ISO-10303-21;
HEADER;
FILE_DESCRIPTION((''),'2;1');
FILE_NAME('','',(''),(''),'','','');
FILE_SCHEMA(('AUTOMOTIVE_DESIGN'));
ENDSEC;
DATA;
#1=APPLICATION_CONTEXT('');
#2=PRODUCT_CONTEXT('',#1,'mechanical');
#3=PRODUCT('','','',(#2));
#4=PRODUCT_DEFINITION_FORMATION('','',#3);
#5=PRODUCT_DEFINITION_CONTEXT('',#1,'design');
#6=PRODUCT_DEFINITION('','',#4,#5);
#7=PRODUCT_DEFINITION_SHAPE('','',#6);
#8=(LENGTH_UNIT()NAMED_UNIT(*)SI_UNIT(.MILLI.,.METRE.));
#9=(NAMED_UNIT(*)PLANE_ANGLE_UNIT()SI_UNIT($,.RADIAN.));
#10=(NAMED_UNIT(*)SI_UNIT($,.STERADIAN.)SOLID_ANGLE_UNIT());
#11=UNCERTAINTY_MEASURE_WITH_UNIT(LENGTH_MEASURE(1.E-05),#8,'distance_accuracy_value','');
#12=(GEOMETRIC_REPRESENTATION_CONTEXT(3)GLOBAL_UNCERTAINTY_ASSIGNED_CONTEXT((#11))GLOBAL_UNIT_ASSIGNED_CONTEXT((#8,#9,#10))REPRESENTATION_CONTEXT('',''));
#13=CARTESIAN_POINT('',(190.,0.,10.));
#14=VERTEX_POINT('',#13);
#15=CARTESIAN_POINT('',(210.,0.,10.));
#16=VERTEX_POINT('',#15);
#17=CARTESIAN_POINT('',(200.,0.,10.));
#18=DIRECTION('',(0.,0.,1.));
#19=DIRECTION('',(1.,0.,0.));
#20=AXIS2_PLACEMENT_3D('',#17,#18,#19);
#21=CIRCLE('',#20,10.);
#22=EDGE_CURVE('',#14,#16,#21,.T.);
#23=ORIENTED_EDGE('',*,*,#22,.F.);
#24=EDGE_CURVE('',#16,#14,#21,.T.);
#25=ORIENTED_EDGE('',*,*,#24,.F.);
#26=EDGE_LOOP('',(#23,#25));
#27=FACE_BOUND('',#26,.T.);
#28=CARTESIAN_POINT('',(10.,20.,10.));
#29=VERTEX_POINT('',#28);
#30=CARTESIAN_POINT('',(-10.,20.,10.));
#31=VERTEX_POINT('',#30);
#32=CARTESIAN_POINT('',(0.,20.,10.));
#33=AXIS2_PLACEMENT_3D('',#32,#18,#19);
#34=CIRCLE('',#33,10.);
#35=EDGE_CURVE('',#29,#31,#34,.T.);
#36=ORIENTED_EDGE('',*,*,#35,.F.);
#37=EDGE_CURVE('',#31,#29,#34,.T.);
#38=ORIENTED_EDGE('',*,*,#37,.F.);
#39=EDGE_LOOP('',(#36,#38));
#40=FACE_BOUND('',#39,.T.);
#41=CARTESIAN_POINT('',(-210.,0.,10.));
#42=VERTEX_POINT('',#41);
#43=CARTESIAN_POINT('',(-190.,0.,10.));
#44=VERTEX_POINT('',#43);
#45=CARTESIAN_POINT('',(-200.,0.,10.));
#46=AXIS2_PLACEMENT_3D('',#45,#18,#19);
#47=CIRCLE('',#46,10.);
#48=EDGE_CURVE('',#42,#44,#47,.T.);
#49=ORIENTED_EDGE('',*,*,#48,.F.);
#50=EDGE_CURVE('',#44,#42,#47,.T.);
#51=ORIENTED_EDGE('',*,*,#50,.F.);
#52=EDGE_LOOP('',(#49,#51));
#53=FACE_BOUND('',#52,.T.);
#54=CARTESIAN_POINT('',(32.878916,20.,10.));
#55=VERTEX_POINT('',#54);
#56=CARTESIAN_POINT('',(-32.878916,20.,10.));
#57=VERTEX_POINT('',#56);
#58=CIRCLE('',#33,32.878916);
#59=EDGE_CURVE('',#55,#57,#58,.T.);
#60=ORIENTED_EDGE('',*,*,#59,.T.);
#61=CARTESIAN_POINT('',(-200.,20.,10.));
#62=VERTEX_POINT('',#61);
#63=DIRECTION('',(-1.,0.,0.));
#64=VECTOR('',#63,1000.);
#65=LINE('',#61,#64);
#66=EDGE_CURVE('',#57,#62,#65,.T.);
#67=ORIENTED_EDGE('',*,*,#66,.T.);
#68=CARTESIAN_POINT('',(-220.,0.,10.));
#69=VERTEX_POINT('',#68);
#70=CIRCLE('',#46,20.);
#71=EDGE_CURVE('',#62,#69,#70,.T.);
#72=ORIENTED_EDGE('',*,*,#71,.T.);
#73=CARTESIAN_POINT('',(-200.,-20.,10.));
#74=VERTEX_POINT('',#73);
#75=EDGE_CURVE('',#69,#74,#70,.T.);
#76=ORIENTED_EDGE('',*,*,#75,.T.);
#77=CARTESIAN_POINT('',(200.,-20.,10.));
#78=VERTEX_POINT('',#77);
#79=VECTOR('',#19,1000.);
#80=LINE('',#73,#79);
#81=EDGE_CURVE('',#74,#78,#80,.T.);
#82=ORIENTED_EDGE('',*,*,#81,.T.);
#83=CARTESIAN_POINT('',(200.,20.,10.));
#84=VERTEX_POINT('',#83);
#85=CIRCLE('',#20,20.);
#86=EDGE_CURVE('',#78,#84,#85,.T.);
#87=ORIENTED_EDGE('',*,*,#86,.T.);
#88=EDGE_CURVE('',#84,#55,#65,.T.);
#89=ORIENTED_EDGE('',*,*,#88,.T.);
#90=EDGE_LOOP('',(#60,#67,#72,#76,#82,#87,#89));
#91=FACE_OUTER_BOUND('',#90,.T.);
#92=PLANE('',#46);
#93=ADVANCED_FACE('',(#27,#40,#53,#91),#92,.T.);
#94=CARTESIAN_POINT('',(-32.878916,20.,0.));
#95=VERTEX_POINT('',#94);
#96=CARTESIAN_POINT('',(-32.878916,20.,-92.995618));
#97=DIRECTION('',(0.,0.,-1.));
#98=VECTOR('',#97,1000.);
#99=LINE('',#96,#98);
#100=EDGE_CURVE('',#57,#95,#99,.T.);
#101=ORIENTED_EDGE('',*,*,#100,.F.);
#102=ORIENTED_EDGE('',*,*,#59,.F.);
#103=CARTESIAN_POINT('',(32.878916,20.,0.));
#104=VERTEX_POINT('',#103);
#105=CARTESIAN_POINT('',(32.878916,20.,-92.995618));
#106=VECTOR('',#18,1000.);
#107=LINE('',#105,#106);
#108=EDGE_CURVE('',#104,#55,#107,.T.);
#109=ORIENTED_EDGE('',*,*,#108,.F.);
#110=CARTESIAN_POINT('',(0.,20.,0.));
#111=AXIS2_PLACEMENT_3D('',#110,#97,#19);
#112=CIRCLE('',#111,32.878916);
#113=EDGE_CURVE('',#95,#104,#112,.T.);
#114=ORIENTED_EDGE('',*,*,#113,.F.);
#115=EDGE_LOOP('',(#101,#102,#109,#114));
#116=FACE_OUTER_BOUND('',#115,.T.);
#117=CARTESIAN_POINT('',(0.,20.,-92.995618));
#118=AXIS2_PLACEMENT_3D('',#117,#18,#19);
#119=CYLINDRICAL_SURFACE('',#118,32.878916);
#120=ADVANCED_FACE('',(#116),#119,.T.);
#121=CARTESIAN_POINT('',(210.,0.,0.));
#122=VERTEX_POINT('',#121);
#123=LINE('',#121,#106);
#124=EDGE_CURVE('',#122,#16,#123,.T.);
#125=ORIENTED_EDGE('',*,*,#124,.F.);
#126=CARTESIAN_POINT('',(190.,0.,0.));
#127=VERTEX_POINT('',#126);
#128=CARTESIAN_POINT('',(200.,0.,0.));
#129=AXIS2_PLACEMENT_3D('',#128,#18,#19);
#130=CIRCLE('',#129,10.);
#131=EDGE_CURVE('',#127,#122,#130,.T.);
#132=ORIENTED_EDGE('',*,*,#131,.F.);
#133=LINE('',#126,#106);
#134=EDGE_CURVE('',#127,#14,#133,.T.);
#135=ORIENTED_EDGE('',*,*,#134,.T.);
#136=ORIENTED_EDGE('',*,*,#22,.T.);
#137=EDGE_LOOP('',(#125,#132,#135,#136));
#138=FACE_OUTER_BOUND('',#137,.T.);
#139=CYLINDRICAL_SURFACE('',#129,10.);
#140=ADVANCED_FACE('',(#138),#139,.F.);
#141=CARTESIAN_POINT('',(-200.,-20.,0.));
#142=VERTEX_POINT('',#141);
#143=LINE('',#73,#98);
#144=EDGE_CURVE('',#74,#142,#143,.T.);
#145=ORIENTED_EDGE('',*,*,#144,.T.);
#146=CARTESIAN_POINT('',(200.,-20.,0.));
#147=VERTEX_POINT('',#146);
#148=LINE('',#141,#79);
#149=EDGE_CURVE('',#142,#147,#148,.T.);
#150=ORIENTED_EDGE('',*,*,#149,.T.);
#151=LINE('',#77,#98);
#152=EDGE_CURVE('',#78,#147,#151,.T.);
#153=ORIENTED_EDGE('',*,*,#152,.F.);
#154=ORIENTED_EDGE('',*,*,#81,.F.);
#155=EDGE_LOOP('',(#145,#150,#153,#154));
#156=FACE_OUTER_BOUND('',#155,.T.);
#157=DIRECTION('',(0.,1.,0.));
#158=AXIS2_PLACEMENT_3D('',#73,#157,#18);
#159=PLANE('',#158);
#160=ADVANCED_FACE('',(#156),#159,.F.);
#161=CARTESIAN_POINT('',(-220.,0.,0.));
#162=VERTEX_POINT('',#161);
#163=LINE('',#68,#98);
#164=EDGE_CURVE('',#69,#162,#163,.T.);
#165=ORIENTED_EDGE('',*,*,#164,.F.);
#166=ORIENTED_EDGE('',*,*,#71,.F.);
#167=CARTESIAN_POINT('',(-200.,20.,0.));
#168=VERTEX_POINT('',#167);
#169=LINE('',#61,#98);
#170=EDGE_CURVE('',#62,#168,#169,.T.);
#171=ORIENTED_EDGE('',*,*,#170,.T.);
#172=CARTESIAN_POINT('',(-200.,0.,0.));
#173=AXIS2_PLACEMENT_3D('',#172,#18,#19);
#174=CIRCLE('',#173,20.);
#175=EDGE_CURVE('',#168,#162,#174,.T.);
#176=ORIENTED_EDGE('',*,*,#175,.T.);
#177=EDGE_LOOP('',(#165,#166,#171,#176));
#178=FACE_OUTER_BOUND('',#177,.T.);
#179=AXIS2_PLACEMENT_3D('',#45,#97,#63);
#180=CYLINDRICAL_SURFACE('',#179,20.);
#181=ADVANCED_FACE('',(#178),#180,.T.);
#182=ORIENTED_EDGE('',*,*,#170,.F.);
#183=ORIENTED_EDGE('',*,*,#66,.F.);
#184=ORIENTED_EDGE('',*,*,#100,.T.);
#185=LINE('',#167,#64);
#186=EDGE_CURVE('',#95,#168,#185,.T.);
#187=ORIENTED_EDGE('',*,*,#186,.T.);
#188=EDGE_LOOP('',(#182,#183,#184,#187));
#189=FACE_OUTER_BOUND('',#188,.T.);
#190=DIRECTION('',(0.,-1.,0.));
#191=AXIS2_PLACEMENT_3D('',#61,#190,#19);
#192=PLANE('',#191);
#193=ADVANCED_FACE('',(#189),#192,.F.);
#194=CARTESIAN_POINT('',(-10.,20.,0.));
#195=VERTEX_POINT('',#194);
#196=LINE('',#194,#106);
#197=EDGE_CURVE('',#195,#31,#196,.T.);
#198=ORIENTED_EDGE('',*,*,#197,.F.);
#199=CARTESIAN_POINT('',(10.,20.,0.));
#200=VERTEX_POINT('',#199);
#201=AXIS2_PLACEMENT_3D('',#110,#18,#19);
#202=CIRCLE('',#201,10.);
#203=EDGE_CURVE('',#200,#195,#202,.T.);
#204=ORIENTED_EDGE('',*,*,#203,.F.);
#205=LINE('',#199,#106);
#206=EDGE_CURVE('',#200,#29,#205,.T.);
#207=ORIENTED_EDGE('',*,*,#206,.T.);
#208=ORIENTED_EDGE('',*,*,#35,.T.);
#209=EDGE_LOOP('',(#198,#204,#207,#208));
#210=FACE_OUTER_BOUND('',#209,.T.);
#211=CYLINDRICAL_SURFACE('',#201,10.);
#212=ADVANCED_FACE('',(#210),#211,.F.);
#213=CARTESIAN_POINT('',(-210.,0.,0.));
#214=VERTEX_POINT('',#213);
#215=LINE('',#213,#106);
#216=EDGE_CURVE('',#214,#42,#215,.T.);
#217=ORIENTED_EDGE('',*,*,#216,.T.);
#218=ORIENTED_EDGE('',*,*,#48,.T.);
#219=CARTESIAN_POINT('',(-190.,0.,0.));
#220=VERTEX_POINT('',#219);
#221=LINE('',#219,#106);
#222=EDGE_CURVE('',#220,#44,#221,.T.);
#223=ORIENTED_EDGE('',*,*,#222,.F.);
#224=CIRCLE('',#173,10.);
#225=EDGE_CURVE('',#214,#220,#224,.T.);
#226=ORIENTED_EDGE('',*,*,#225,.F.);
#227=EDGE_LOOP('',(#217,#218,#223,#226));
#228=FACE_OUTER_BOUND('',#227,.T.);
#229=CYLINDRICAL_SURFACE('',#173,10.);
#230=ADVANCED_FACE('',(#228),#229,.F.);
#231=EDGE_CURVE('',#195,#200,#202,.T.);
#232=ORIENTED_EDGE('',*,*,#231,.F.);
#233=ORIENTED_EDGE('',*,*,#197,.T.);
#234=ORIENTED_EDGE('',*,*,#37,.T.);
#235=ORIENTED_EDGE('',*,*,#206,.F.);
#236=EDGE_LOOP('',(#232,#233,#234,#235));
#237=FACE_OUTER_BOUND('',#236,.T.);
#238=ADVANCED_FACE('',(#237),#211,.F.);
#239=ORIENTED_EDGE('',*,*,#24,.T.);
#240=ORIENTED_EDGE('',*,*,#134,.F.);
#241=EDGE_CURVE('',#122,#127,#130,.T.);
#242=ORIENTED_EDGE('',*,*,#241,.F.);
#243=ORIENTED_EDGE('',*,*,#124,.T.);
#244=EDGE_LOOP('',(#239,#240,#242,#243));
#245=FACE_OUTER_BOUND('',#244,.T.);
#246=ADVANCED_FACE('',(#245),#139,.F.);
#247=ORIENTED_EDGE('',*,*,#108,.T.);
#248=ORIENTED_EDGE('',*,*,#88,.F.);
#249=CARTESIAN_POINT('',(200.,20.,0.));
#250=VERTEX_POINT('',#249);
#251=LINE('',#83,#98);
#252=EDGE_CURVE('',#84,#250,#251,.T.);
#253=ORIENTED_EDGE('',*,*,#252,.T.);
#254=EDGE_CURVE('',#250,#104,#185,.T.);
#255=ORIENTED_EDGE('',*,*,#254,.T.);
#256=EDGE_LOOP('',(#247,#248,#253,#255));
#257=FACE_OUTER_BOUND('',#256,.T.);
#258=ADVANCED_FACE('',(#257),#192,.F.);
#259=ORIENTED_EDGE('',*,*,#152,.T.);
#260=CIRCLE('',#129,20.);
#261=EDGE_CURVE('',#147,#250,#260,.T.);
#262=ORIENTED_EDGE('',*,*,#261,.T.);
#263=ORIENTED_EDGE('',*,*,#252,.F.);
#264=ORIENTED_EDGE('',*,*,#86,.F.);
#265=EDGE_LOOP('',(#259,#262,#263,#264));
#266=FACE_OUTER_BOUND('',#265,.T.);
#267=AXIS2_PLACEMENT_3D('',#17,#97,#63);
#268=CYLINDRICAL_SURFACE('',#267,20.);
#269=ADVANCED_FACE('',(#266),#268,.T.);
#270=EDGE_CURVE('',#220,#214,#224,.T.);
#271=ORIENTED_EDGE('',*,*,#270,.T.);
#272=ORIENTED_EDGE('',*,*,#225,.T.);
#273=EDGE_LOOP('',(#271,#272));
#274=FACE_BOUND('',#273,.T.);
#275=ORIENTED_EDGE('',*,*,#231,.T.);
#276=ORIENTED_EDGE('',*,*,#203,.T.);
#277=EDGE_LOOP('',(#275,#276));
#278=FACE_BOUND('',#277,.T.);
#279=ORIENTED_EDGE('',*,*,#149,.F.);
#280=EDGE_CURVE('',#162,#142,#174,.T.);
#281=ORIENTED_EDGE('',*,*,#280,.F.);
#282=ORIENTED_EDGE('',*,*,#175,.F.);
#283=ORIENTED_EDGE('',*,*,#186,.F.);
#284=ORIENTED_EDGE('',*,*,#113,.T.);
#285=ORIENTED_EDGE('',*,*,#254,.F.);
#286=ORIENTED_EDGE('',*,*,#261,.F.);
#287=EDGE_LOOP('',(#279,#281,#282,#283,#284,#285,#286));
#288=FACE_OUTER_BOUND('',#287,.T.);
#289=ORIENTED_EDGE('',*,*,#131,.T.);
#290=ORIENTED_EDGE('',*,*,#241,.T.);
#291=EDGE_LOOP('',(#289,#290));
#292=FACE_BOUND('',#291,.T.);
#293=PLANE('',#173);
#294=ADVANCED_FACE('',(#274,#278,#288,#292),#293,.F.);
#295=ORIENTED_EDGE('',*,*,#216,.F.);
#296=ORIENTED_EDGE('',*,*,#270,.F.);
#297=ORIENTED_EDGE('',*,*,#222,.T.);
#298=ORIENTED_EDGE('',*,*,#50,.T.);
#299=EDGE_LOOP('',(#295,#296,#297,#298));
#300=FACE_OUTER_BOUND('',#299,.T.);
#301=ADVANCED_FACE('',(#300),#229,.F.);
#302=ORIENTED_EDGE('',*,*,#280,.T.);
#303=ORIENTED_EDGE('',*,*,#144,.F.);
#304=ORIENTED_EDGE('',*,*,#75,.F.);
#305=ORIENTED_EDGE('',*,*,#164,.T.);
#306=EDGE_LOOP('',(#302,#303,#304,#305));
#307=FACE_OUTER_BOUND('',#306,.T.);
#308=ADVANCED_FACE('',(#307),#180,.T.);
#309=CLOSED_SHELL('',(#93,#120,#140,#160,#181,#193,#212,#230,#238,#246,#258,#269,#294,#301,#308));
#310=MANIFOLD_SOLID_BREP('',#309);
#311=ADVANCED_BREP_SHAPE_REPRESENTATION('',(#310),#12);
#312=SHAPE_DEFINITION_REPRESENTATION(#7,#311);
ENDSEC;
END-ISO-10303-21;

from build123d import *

# Parameters (mm, degrees)
BOSS_EXTRUDE1_DEPTH = 10
SKETCH2_R           = 10
CUT_EXTRUDE1_DEPTH  = 222.133443875
SKETCH4_R           = 32.878916004
BOSS_EXTRUDE2_DEPTH = 10
SKETCH5_R           = 10
CUT_EXTRUDE3_DEPTH  = 227.48659951


with BuildPart() as part:
    # Sketch1 → Boss-Extrude1 (new body)
    with BuildSketch(Plane.XY):
        with BuildLine():
            Line((-200, 20), (200, 20))
            ThreePointArc((200, 20), (220, 0), (200, -20))
            Line((200, -20), (-200, -20))
            ThreePointArc((-200, -20), (-220, 0), (-200, 20))
        make_face()
    extrude(amount=BOSS_EXTRUDE1_DEPTH)

    # Sketch2 → Cut-Extrude1 (cut, through all)
    with BuildSketch(Plane.XY.offset(10)):
        with Locations((-200, 0)):
            Circle(SKETCH2_R)
        with Locations((200, 0)):
            Circle(SKETCH2_R)
    extrude(amount=-CUT_EXTRUDE1_DEPTH, mode=Mode.SUBTRACT)

    # Sketch4 → Boss-Extrude2 (add)
    with BuildSketch(Plane.XY.offset(10)):
        with Locations((0, 20)):
            Circle(SKETCH4_R)
    extrude(amount=-BOSS_EXTRUDE2_DEPTH)

    # Sketch5 → Cut-Extrude3 (cut, through all)
    with BuildSketch(Plane.XY.offset(10)):
        with Locations((0, 20)):
            Circle(SKETCH5_R)
    extrude(amount=-CUT_EXTRUDE3_DEPTH, mode=Mode.SUBTRACT)


solid = part.part
